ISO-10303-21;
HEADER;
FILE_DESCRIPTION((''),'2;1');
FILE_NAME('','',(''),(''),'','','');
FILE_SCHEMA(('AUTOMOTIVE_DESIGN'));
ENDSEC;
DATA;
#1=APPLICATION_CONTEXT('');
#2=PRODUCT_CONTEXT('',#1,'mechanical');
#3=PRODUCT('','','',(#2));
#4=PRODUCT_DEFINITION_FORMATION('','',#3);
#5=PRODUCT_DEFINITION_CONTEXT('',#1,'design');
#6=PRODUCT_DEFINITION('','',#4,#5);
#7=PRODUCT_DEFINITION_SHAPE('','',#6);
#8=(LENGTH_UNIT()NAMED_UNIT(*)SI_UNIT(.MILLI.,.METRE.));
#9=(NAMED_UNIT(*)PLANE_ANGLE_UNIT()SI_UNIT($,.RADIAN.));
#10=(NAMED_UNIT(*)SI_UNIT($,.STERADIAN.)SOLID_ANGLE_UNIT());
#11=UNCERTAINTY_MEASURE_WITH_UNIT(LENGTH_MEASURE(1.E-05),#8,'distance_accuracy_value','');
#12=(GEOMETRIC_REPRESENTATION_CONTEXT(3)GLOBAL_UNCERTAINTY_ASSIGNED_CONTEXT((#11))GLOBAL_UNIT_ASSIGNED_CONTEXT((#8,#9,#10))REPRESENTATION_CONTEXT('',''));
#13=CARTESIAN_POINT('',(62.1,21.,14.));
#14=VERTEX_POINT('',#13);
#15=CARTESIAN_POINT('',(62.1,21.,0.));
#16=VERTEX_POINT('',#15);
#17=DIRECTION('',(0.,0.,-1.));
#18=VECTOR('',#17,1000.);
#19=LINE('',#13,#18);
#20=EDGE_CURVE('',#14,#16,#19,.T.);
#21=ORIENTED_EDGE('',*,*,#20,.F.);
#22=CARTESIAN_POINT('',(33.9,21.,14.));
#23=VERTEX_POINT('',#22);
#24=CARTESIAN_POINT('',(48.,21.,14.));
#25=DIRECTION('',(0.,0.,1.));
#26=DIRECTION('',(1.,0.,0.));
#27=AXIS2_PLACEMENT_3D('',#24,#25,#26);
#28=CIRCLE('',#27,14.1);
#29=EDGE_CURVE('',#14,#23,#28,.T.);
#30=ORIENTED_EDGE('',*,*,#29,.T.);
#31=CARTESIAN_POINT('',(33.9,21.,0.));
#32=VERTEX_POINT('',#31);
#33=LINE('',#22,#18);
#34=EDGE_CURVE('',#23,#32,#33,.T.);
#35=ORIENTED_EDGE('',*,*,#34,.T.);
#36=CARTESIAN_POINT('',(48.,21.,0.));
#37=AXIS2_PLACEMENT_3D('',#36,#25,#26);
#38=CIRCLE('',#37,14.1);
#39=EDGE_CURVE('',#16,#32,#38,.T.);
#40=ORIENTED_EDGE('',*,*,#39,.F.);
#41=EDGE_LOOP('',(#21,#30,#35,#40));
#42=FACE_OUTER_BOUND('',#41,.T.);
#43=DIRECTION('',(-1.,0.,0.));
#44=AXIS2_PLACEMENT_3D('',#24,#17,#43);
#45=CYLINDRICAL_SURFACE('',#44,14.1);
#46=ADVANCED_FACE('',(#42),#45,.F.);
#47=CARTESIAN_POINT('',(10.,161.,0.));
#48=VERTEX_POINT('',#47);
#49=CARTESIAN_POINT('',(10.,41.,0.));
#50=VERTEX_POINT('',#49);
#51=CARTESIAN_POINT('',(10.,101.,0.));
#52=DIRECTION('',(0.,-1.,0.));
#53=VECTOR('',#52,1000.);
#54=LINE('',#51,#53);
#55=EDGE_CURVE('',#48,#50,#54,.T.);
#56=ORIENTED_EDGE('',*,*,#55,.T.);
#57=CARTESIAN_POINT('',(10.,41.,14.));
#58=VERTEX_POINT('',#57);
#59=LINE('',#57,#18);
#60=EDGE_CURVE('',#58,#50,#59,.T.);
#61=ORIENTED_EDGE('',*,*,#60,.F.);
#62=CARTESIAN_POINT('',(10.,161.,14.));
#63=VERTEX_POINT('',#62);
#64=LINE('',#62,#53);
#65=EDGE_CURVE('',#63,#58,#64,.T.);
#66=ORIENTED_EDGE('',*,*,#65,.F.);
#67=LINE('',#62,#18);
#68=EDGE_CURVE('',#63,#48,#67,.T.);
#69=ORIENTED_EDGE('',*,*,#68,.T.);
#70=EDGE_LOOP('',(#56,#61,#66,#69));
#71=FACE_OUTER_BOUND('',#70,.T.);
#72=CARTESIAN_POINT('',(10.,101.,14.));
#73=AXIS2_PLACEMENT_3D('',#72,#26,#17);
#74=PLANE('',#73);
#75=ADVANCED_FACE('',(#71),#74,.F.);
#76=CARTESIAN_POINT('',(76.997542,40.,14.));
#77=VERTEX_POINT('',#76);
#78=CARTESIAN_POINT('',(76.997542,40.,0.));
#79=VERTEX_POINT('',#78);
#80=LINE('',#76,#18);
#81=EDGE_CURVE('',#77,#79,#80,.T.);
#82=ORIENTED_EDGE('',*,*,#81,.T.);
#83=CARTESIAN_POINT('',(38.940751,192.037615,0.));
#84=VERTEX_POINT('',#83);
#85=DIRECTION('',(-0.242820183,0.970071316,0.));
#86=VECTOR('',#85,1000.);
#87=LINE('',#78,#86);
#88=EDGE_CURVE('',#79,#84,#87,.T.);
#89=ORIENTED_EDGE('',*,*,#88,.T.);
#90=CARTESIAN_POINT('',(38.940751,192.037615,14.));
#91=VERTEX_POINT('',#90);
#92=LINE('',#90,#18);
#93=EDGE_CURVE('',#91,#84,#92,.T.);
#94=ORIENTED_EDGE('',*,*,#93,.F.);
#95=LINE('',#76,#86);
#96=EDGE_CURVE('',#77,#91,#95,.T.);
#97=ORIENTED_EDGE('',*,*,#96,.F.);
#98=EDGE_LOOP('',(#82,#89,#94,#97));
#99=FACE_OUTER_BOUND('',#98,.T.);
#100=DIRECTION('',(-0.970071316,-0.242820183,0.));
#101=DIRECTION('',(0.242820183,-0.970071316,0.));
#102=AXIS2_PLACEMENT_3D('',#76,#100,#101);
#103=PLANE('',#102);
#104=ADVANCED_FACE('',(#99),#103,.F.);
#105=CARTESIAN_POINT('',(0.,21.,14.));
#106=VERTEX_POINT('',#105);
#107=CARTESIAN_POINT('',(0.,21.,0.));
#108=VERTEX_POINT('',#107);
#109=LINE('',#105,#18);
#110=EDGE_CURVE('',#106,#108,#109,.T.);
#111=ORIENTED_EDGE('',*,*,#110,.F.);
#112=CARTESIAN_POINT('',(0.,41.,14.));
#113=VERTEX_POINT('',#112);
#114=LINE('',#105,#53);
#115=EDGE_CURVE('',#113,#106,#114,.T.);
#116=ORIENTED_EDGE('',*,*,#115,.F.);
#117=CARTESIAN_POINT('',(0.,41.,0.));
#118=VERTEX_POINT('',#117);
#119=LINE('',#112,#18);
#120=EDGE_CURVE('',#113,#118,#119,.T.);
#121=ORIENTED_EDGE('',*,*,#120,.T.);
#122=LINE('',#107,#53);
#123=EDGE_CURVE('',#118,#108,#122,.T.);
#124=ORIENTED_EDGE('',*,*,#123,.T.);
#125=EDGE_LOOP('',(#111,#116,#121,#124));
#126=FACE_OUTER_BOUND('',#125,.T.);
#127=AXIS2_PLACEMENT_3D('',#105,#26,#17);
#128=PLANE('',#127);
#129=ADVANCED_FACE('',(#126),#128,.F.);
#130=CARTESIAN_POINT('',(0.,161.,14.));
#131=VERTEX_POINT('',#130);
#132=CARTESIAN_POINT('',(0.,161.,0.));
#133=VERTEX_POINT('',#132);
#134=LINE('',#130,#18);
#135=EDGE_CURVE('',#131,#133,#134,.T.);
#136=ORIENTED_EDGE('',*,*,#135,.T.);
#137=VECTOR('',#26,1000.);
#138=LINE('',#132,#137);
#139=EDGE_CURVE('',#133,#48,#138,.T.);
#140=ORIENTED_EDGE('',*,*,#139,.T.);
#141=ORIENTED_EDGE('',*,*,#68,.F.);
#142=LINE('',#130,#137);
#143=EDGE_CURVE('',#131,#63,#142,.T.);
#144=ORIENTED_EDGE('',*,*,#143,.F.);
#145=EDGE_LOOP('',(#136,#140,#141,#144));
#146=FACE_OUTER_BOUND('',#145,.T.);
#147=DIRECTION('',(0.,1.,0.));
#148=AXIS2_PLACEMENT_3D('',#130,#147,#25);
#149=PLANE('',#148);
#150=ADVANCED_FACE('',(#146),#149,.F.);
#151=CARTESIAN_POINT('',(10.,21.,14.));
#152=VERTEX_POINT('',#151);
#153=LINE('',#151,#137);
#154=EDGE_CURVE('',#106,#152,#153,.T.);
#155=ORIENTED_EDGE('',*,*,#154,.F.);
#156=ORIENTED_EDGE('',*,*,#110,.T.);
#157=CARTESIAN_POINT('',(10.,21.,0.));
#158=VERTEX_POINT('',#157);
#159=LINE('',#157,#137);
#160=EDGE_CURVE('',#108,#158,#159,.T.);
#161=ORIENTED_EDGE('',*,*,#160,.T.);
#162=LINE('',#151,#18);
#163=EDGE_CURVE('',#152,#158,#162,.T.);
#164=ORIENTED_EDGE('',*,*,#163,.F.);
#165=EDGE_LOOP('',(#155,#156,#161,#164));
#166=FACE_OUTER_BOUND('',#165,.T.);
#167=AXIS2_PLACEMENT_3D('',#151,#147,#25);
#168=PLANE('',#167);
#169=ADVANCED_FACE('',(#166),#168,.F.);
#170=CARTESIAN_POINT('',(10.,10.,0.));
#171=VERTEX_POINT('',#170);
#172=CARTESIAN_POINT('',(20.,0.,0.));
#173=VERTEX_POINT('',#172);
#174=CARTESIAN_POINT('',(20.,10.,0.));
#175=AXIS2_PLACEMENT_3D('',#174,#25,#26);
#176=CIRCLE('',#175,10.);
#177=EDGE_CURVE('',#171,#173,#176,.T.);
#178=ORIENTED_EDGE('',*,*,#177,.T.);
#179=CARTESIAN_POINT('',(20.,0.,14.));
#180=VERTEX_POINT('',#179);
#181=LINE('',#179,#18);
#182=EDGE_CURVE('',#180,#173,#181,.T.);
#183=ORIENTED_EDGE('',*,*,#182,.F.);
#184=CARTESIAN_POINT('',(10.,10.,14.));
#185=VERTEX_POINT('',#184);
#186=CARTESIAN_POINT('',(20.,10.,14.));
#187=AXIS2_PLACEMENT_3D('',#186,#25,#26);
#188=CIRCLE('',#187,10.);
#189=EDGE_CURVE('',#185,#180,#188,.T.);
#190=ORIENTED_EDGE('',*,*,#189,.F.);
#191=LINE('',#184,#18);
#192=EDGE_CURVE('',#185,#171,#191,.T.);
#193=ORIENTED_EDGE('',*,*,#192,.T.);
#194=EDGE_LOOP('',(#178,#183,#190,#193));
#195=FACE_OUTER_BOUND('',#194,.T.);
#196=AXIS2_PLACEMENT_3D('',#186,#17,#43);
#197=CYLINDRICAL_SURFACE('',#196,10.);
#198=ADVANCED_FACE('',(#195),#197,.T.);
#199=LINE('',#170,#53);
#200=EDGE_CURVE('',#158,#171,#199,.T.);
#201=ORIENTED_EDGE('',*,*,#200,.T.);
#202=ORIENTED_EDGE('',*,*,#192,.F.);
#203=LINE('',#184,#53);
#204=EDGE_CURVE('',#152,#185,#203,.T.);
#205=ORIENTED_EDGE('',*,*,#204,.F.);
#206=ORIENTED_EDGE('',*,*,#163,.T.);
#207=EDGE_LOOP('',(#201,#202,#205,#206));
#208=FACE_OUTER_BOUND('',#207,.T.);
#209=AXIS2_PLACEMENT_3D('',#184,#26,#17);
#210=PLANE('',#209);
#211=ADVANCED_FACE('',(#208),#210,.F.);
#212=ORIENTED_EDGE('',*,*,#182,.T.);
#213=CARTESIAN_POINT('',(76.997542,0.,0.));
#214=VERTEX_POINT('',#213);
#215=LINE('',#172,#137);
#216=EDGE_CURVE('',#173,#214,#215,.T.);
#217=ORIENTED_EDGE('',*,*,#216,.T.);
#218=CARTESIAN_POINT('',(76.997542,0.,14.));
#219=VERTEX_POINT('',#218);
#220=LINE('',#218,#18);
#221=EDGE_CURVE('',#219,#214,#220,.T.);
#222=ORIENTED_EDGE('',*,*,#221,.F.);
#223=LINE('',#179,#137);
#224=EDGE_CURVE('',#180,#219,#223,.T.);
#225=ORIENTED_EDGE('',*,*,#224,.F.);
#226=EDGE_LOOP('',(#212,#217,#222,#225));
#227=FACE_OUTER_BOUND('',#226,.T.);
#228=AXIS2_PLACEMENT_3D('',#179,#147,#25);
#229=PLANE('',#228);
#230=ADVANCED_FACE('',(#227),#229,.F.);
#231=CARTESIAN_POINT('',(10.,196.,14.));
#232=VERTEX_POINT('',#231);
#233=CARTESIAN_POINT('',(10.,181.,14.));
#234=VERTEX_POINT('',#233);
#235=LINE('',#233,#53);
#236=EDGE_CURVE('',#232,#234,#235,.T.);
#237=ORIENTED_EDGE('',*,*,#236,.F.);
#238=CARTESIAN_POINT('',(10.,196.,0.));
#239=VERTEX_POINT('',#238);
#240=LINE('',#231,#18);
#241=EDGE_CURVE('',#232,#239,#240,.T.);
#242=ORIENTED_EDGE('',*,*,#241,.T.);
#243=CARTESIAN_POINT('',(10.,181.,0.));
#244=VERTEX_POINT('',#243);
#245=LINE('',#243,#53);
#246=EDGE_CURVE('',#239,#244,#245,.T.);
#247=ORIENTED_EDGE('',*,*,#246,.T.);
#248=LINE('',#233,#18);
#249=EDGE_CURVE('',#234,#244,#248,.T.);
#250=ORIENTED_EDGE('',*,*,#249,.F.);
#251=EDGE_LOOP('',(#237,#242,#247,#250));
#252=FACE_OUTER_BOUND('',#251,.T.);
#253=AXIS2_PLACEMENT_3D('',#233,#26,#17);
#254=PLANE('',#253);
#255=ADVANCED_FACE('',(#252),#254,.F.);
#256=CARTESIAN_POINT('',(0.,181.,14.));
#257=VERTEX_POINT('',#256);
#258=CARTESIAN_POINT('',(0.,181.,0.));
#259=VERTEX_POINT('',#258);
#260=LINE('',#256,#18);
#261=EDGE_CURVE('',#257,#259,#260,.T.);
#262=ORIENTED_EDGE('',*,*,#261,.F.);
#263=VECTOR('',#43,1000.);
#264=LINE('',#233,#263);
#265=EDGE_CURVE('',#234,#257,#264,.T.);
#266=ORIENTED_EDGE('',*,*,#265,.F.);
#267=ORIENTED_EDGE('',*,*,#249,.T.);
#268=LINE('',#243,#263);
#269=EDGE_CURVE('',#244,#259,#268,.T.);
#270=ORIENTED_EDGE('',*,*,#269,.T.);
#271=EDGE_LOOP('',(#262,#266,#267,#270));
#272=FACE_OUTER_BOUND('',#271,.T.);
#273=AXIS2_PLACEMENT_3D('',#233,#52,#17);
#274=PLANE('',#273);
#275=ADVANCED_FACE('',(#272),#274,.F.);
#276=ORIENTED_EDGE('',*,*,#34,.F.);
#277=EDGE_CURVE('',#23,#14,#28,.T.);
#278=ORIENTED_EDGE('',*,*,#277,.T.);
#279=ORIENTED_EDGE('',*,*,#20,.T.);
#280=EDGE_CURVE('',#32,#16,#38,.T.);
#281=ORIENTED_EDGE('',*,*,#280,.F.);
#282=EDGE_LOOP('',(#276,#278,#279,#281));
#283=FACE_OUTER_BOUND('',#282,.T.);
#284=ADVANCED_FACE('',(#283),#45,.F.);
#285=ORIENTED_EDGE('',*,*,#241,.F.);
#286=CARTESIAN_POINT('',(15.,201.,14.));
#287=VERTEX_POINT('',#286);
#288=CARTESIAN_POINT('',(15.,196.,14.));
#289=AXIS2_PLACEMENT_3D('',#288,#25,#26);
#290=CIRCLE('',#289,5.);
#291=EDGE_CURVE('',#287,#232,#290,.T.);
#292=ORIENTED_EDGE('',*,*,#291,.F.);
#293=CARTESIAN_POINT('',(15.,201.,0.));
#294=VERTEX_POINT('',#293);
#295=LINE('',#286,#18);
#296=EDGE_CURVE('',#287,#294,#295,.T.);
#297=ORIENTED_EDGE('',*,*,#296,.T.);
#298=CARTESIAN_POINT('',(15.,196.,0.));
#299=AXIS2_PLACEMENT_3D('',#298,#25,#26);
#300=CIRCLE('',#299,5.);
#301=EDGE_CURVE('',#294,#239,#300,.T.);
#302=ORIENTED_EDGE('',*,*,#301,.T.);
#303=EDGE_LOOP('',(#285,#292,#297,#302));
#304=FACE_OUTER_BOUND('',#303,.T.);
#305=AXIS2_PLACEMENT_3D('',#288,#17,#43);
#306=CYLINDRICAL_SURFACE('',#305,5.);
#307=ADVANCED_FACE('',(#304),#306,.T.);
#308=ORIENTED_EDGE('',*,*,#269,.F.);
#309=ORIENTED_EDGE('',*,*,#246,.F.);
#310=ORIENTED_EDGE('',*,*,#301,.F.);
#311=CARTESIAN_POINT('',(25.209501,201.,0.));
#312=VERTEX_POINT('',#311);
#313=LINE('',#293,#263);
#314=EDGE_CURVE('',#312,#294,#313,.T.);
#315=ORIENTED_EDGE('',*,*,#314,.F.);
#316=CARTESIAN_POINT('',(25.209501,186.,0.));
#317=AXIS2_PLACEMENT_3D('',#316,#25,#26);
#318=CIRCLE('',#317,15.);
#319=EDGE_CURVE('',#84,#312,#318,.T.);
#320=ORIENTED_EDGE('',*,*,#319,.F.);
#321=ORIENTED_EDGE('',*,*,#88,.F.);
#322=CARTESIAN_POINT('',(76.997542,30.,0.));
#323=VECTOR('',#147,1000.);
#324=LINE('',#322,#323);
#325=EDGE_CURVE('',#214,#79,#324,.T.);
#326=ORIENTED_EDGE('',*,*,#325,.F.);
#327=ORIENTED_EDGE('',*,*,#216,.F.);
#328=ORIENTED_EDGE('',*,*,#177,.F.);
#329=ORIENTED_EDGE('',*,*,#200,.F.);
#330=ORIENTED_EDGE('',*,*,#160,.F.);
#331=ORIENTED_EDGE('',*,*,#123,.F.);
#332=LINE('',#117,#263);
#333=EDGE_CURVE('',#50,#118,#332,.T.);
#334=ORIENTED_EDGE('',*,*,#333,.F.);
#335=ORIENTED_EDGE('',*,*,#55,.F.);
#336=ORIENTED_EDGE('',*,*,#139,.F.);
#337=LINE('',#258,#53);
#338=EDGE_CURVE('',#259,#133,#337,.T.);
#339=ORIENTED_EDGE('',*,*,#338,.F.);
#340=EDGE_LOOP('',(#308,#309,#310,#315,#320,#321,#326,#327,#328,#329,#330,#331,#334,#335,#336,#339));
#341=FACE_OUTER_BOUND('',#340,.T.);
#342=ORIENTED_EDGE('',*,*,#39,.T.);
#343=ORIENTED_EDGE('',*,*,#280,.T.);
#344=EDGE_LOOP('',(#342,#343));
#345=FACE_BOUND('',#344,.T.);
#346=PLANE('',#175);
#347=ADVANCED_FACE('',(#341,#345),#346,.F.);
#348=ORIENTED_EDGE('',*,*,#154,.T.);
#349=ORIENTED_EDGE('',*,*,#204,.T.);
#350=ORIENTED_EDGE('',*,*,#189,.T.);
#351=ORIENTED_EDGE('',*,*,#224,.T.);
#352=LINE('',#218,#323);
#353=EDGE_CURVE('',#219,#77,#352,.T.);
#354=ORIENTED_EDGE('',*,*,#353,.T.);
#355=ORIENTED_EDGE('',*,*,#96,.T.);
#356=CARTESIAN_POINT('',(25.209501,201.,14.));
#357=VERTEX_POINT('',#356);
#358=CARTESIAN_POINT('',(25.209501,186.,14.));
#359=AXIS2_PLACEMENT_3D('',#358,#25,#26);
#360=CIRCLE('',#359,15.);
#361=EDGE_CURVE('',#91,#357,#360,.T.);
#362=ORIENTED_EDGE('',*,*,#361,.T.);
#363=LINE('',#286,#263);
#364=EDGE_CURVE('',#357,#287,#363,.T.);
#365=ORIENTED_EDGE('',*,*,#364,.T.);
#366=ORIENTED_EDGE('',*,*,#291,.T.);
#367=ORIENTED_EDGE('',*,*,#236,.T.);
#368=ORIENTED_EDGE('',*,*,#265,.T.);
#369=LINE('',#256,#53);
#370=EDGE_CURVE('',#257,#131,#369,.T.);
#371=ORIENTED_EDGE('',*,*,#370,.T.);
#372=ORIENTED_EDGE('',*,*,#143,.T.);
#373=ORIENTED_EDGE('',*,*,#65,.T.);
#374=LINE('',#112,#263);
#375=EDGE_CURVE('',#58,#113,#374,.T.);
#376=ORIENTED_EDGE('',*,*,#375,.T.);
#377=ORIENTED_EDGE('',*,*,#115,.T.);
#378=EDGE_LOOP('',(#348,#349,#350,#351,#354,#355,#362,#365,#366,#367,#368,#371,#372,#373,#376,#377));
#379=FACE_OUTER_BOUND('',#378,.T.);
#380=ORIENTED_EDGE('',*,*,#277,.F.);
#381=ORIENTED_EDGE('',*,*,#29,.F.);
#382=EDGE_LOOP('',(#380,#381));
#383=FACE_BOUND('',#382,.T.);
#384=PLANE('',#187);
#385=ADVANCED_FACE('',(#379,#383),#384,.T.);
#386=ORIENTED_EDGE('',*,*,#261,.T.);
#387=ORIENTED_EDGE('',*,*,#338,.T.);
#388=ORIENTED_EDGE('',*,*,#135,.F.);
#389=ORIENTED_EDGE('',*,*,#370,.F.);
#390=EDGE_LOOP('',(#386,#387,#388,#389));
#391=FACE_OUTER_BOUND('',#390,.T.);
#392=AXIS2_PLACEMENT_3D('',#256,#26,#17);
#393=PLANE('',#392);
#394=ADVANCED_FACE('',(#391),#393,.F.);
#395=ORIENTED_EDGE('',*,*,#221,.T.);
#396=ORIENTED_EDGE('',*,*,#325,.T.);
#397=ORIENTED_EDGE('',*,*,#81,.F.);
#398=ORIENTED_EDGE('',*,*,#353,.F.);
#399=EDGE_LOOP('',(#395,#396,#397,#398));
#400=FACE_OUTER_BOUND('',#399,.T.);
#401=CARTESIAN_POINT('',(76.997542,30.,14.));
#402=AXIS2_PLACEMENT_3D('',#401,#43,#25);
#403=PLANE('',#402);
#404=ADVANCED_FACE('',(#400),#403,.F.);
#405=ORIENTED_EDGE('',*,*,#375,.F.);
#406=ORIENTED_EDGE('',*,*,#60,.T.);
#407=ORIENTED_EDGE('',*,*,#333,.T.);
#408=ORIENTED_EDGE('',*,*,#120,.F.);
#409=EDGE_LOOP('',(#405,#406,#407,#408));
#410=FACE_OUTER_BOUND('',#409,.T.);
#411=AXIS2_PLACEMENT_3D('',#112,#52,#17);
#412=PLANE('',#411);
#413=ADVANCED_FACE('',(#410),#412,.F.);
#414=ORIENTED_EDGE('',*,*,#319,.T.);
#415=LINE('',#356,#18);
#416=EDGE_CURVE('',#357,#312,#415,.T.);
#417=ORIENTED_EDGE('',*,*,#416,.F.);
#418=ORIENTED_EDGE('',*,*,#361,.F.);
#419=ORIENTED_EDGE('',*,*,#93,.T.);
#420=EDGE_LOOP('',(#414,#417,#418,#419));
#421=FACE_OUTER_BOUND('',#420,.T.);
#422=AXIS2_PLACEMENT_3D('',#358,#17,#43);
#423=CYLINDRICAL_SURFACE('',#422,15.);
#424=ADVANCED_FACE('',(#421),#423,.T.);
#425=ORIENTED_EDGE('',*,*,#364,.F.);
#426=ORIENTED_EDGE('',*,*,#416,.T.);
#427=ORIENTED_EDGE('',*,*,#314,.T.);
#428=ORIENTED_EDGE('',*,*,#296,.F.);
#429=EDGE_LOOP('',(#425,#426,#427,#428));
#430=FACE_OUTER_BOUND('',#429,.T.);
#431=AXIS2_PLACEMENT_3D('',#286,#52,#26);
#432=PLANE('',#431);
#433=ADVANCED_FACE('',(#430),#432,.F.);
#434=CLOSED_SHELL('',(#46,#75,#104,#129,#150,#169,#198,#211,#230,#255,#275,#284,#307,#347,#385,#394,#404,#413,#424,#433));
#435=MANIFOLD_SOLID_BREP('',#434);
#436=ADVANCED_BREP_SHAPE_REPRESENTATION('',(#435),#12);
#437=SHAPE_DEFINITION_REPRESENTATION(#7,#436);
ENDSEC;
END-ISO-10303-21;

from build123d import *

# Parameters (mm, degrees)
SKETCH2_R           = 14.1
BOSS_EXTRUDE2_DEPTH = 14


with BuildPart() as part:
    # Sketch2 → Boss-Extrude2 (new body)
    with BuildSketch(Plane.XY):
        with BuildLine():
            Line((10, 181), (10, 196))
            ThreePointArc((10, 196), (11.464466094, 199.535533906), (15, 201))
            Line((15, 201), (25.209501406, 201))
            ThreePointArc((25.209501406, 201), (33.408153022, 198.561134968), (38.940750673, 192.037614891))
            Line((38.940750673, 192.037614891), (76.997541741, 40))
            Line((76.997541741, 40), (76.997541741, 30))
            Line((76.997541741, 30), (76.997541741, 10))
            Line((76.997541741, 10), (76.997541741, 0))
            Line((76.997541741, 0), (20, 0))
            ThreePointArc((20, 0), (12.928932188, 2.928932188), (10, 10))
            Line((10, 10), (10, 21))
            Line((10, 21), (0, 21))
            Line((0, 21), (0, 41))
            Line((0, 41), (10, 41))
            Line((10, 41), (10, 101))
            Line((10, 101), (10, 161))
            Line((10, 161), (0, 161))
            Line((0, 161), (0, 181))
            Line((0, 181), (10, 181))
        make_face()
        with Locations((48, 21)):
            Circle(SKETCH2_R, mode=Mode.SUBTRACT)
    extrude(amount=BOSS_EXTRUDE2_DEPTH)


solid = part.part
